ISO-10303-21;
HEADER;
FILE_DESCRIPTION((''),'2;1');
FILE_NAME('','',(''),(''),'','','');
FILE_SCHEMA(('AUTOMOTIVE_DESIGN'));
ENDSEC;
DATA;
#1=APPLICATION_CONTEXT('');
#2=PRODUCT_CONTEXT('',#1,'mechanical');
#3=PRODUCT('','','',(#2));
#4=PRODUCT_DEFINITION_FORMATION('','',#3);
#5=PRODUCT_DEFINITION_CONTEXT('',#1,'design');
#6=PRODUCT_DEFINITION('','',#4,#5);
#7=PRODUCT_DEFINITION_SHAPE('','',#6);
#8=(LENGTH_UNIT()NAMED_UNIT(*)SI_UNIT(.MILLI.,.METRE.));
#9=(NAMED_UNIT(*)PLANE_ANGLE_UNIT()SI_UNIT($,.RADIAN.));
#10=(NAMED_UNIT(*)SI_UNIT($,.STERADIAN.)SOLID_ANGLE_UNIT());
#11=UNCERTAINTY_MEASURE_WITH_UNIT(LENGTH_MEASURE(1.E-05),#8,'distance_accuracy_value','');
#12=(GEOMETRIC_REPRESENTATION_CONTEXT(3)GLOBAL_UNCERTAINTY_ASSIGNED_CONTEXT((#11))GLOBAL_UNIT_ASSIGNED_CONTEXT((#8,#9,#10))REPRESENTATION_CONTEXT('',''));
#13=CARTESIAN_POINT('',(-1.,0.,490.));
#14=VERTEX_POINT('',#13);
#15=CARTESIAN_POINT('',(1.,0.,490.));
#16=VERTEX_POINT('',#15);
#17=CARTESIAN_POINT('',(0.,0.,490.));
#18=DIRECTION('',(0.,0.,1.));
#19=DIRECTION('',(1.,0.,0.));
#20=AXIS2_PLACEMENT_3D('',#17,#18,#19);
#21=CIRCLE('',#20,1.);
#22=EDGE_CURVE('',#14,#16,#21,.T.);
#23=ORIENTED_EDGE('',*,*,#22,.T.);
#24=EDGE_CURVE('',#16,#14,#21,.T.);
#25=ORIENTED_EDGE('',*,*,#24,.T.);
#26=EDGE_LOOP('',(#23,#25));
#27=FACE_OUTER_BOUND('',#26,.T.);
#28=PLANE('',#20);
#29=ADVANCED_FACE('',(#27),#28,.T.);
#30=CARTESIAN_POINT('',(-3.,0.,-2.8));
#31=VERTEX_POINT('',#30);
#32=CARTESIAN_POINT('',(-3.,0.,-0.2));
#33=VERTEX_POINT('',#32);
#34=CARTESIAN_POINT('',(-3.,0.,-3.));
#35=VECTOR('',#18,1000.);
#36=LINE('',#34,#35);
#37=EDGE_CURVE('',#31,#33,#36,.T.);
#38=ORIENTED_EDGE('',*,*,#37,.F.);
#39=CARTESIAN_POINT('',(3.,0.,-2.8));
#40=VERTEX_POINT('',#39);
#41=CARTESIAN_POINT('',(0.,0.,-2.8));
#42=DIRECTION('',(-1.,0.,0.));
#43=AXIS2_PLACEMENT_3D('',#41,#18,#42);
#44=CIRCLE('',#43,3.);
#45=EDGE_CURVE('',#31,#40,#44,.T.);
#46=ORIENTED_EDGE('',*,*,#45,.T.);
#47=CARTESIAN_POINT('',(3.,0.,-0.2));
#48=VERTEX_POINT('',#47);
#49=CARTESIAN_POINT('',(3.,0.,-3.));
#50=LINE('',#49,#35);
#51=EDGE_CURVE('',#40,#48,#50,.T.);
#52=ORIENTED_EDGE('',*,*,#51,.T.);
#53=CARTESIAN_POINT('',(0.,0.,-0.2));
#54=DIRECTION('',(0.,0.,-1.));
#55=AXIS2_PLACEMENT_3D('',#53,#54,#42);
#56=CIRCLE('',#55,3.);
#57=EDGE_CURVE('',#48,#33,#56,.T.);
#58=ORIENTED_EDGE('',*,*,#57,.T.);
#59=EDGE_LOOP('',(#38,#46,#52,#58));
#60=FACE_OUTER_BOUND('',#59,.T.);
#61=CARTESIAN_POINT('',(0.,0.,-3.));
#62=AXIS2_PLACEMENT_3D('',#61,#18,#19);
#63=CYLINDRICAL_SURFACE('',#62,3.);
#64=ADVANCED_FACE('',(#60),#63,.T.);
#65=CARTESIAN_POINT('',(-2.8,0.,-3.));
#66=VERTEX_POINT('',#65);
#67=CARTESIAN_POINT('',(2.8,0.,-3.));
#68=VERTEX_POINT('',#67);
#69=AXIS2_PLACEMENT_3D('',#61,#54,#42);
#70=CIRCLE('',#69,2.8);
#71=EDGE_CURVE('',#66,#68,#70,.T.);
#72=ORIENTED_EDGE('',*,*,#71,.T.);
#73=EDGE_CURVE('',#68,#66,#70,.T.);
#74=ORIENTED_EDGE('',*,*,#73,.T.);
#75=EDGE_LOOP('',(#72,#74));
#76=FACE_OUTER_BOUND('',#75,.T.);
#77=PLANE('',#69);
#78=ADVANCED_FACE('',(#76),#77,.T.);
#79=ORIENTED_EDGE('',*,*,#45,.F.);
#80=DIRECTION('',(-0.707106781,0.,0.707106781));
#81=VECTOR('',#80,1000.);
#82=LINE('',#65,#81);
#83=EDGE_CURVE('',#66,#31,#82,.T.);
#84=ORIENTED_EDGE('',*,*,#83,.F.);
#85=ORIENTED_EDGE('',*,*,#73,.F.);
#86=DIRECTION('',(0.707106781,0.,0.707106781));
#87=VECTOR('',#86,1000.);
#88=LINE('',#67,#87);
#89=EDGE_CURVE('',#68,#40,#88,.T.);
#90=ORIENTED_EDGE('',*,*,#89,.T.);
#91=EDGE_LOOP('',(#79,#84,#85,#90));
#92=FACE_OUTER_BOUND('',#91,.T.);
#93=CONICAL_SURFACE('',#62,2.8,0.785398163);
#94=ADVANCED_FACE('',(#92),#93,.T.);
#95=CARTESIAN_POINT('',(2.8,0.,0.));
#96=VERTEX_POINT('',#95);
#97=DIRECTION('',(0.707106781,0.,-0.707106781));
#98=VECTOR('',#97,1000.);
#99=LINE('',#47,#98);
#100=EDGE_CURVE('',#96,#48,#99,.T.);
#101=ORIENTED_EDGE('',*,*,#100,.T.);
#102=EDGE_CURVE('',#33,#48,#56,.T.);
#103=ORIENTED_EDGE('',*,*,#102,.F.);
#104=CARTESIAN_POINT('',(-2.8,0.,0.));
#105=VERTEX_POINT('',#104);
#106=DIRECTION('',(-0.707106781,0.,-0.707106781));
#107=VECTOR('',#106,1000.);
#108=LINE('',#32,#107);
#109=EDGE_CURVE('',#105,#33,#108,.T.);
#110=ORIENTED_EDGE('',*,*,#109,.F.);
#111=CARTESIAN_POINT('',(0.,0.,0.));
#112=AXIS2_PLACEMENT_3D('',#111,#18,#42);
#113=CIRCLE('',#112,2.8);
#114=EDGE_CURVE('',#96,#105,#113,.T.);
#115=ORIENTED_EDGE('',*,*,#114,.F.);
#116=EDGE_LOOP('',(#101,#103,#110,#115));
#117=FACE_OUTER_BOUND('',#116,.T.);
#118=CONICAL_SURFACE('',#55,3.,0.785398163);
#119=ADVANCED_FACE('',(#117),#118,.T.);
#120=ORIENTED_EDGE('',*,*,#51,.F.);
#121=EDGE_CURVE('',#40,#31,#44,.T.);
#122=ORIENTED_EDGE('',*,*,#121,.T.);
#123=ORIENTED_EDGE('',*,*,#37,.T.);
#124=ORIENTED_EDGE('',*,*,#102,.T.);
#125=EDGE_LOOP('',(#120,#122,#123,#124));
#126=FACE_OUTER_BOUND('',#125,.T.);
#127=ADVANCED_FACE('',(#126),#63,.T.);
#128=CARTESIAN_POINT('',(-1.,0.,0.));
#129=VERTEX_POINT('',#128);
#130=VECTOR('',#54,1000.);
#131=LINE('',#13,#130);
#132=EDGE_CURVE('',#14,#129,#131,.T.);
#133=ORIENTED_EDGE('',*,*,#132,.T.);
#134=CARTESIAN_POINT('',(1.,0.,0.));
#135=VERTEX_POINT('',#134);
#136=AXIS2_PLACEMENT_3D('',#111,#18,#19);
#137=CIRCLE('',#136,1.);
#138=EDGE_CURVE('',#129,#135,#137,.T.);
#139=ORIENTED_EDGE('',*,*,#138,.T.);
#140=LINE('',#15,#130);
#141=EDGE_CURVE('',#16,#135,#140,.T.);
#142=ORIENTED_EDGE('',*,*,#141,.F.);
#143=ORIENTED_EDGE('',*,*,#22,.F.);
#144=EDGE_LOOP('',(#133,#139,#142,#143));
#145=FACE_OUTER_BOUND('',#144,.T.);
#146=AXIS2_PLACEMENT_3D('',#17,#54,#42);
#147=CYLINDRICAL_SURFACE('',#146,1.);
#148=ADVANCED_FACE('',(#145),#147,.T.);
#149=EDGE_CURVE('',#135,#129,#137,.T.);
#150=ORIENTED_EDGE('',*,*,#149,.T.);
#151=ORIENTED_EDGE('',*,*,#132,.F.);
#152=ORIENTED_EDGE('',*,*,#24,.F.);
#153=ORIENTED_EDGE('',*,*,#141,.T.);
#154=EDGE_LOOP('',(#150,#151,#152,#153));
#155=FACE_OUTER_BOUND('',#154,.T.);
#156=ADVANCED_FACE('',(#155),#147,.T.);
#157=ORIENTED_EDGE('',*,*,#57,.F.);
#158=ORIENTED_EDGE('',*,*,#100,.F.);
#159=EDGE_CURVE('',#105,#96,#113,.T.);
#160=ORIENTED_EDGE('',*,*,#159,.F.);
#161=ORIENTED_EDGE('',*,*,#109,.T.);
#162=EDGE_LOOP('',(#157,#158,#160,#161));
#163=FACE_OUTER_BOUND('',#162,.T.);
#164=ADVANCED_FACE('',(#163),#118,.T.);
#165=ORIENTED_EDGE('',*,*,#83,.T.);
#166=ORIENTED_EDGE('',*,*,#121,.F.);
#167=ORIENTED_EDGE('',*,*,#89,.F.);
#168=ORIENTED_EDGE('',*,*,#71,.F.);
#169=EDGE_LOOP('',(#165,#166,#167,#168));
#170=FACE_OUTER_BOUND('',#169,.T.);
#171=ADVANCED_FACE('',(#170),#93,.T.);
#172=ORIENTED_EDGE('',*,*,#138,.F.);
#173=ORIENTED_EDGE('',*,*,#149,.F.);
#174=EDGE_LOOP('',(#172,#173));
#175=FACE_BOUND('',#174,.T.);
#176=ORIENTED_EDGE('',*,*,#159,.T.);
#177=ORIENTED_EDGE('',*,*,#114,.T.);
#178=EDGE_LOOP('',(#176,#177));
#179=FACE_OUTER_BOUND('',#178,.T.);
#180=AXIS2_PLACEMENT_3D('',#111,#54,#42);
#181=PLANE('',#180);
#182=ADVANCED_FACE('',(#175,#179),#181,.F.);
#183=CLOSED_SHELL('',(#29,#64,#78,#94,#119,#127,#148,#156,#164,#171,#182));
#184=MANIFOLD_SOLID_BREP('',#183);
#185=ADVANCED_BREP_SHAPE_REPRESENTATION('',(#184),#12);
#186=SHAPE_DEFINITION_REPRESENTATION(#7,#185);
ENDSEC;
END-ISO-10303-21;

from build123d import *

# Parameters (mm, degrees)
SKETCH1_R           = 1
BOSS_EXTRUDE1_DEPTH = 490
SKETCH2_R           = 3
BOSS_EXTRUDE2_DEPTH = 3
CHAMFER1_SIZE       = 0.2


with BuildPart() as part:
    # Sketch1 → Boss-Extrude1 (new body)
    with BuildSketch(Plane.XY):
        Circle(SKETCH1_R)
    extrude(amount=BOSS_EXTRUDE1_DEPTH)

    # Sketch2 → Boss-Extrude2 (add)
    with BuildSketch(Plane(origin=(0, 0, 0), x_dir=(-1, 0, 0), z_dir=(0, 0, -1))):
        Circle(SKETCH2_R)
    extrude(amount=BOSS_EXTRUDE2_DEPTH)

    # Chamfer1
    chamfer1_edges = [part.edges().sort_by_distance(p)[0] for p in [
        (3, 0, 0),
        (3, 0, -3),
    ]]
    chamfer(chamfer1_edges, length=CHAMFER1_SIZE)


solid = part.part
